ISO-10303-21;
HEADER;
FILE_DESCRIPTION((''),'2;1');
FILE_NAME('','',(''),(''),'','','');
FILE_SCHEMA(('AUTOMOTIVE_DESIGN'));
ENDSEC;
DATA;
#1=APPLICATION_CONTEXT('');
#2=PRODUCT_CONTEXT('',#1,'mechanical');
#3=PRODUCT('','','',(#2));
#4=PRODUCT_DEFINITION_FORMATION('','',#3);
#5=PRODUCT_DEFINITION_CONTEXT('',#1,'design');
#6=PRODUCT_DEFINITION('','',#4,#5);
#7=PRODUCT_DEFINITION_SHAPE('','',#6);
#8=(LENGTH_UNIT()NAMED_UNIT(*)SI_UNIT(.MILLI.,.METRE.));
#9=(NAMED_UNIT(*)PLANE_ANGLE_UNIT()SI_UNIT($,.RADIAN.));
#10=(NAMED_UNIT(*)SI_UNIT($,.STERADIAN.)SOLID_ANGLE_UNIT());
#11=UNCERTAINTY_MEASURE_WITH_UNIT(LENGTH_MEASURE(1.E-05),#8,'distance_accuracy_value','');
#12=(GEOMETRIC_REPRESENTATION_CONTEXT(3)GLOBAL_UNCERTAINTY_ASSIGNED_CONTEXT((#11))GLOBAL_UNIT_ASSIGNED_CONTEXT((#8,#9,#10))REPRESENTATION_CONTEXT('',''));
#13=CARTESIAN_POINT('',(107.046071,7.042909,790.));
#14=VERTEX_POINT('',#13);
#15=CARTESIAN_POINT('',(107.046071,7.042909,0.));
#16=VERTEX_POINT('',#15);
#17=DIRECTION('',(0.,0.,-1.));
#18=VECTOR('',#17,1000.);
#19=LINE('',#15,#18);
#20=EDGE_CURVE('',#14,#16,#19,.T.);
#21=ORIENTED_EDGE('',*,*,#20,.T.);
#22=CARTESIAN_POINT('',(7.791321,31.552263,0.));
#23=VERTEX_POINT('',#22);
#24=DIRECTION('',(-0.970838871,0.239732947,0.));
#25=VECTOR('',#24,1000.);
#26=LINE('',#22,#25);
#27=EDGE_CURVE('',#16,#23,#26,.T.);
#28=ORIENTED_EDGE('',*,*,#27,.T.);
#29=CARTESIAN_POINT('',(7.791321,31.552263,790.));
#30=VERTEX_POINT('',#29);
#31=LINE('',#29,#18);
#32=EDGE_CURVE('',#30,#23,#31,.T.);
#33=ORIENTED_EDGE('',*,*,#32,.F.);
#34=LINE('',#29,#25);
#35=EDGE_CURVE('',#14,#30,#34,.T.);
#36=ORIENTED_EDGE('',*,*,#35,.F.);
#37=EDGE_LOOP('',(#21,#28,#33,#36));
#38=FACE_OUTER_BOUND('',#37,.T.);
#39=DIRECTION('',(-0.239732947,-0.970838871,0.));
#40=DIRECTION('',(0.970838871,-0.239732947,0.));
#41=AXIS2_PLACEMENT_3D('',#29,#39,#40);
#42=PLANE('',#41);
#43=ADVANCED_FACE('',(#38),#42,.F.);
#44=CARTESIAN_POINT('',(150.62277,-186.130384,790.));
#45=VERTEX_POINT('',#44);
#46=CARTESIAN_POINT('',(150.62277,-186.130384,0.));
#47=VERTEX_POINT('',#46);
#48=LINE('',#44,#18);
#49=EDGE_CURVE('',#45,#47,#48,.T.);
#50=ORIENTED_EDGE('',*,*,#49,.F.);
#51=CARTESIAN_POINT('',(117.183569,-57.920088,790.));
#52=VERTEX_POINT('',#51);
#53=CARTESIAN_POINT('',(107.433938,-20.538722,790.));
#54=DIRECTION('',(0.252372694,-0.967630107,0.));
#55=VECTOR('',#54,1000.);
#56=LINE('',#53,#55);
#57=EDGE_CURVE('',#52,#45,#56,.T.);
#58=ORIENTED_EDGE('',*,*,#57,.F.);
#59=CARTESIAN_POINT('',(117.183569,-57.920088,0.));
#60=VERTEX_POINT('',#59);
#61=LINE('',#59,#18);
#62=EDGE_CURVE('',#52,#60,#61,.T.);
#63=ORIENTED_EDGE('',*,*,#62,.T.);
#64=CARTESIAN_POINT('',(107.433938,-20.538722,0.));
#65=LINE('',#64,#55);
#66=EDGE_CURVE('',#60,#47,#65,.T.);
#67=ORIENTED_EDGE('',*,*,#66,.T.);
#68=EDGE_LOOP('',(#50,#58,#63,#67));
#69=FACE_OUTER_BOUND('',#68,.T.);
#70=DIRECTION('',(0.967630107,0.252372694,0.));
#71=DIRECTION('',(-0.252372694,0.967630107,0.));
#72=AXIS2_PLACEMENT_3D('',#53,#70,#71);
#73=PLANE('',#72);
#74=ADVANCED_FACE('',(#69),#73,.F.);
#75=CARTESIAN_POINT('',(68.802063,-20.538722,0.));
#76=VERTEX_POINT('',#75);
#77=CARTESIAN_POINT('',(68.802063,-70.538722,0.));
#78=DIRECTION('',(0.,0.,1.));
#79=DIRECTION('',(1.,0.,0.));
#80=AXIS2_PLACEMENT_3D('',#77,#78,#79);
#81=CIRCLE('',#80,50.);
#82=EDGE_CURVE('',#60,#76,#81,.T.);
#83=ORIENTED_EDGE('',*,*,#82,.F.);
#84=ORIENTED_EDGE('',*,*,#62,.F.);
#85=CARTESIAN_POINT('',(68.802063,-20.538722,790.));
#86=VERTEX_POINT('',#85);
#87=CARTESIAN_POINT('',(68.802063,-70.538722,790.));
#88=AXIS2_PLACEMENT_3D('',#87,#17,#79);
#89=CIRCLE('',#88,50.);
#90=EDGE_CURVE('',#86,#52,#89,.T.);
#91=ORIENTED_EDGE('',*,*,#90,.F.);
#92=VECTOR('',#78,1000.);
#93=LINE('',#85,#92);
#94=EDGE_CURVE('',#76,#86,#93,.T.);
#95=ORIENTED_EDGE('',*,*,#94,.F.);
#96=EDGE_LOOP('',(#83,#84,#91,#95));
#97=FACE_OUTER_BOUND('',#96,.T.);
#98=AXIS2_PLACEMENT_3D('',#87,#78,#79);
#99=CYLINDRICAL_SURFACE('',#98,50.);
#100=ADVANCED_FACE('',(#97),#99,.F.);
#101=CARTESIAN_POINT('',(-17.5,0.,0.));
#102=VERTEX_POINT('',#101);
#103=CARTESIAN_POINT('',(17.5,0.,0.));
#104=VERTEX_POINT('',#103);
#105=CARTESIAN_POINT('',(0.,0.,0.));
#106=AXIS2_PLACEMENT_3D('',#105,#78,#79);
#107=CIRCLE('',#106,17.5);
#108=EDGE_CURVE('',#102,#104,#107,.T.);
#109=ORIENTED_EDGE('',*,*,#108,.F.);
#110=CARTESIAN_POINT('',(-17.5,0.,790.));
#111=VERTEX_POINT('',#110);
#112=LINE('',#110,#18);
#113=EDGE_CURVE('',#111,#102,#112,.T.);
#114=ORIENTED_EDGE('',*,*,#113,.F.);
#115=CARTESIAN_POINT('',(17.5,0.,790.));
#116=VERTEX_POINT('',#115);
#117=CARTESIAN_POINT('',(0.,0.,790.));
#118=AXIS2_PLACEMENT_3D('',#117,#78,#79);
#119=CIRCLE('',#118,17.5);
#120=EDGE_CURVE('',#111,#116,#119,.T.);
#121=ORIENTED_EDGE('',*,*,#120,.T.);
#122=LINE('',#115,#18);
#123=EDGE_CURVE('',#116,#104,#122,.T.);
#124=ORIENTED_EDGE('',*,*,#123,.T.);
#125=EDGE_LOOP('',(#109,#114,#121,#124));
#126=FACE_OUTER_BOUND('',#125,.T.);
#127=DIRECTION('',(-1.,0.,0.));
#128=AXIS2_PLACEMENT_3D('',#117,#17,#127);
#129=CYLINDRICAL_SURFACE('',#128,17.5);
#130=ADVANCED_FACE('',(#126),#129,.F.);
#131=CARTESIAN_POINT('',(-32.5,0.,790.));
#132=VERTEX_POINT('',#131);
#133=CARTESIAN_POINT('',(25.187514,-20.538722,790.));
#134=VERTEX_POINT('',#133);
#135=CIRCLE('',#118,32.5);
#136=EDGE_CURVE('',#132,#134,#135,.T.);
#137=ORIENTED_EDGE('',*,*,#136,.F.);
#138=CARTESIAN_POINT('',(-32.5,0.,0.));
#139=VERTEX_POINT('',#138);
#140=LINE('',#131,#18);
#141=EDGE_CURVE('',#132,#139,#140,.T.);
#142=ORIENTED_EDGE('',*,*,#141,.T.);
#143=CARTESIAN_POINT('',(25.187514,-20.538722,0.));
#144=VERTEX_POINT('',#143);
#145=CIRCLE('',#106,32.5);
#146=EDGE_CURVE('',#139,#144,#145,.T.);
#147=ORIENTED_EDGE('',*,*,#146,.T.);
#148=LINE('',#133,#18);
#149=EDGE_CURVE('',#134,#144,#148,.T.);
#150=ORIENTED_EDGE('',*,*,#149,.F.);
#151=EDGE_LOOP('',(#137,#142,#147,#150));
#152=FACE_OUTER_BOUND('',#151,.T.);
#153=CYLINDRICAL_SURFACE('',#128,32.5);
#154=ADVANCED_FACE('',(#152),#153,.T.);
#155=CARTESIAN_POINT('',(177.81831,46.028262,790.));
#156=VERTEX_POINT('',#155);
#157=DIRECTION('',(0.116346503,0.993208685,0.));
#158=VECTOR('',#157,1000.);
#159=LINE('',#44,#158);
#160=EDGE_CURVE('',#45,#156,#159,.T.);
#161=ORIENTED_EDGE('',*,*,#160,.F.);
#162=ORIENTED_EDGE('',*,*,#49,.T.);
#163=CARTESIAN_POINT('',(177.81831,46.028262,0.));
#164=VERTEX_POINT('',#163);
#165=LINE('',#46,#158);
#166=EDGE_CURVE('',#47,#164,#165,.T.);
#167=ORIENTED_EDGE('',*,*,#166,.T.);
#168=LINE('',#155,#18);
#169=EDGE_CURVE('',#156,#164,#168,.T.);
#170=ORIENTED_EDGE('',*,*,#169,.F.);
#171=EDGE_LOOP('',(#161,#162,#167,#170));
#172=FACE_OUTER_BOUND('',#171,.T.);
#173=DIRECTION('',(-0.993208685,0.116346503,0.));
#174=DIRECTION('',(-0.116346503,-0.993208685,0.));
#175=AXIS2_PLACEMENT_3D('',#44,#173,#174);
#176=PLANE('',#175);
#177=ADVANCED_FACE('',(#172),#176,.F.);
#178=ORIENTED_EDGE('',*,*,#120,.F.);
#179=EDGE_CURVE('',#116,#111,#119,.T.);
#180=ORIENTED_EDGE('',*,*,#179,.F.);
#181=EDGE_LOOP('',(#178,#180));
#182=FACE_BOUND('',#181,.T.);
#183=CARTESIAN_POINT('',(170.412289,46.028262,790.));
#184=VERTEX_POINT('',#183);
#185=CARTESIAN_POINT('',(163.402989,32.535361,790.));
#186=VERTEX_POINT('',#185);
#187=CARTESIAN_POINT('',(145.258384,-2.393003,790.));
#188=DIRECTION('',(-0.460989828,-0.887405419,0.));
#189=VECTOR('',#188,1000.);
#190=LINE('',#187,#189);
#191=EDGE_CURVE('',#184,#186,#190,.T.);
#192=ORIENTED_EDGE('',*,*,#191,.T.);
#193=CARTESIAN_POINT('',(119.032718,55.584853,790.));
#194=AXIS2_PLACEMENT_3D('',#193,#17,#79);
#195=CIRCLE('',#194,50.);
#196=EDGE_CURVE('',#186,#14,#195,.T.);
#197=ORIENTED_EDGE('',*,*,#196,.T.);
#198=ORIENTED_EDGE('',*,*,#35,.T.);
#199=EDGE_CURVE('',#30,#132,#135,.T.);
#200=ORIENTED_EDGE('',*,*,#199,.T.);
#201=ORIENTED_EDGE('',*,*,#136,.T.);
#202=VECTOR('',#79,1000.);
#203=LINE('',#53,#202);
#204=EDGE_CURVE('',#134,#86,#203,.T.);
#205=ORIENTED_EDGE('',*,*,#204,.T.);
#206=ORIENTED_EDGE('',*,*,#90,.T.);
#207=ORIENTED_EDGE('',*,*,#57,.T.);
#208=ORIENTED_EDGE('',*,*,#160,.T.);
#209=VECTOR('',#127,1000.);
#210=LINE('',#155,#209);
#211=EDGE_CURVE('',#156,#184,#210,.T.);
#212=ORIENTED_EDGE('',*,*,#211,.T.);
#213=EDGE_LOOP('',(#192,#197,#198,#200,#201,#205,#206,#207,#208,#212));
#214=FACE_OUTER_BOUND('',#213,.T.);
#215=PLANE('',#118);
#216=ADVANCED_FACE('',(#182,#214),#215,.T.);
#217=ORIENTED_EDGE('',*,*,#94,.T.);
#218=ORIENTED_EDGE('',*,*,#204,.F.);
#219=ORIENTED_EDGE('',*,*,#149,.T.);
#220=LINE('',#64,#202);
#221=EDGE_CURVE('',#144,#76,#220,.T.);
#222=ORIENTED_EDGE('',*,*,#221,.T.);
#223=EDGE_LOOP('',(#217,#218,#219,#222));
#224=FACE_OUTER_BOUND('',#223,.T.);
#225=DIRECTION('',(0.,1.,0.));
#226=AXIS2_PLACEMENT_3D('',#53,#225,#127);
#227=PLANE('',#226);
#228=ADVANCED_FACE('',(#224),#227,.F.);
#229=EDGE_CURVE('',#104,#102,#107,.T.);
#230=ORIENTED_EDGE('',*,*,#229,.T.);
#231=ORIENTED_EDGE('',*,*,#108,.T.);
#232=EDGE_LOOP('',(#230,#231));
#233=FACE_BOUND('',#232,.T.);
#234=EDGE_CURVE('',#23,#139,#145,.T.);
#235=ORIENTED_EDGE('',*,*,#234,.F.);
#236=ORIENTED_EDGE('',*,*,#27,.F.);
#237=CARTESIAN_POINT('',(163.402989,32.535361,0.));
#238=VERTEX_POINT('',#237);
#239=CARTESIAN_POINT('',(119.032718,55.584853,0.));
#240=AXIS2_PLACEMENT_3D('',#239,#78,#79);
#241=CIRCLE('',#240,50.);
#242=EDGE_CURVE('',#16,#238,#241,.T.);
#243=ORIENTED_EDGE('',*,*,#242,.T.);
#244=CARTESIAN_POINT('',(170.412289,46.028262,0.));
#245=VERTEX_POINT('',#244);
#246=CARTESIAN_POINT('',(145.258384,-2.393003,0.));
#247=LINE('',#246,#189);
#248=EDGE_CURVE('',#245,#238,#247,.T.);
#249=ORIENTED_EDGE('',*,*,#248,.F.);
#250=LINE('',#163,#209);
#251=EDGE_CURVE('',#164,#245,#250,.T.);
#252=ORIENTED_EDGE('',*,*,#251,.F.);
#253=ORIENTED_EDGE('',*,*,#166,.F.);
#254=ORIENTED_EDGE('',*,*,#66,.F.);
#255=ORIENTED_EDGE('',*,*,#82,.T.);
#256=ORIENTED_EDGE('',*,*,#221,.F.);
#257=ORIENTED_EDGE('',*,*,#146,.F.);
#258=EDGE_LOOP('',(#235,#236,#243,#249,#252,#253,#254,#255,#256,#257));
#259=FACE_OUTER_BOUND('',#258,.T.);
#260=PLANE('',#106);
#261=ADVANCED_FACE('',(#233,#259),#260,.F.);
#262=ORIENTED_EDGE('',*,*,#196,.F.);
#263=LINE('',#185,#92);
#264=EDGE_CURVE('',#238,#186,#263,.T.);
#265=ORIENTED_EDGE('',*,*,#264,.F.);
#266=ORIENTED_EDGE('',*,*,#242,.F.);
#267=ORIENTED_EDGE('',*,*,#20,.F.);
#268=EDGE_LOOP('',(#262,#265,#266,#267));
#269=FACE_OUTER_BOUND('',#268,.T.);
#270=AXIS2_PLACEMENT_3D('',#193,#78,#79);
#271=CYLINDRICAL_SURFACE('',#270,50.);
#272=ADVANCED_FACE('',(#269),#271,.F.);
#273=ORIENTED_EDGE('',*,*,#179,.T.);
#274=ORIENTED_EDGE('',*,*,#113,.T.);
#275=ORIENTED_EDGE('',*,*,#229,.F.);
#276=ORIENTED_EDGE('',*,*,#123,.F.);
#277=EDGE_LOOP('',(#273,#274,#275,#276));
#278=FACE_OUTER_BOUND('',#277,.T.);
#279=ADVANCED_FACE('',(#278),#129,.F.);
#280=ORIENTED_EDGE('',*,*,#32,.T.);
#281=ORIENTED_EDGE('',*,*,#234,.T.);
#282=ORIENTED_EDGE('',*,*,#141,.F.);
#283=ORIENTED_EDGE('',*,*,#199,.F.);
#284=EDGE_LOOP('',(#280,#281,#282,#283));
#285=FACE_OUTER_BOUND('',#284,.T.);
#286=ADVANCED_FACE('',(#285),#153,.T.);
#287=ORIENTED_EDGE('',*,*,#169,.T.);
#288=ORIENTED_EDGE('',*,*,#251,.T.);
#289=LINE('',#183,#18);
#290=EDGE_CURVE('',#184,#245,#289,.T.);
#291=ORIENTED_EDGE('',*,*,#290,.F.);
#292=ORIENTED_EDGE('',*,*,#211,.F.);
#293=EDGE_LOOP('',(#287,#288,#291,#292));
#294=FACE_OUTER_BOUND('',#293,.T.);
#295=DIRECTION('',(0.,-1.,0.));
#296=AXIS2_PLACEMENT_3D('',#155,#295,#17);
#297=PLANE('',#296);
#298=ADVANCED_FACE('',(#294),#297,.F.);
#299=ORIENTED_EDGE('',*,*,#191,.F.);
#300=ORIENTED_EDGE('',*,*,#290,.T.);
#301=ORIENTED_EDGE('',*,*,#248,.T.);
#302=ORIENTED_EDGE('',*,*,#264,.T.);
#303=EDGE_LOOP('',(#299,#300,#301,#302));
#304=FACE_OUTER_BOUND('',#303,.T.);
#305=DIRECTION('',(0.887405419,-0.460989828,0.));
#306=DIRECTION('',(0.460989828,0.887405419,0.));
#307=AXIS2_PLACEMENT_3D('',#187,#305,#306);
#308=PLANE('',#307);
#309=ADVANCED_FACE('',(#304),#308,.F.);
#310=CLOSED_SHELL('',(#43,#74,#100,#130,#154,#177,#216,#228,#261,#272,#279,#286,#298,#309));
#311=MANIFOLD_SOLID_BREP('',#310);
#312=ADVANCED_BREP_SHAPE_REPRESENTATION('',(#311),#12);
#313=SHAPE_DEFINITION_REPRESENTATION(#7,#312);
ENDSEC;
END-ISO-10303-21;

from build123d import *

# Parameters (mm, degrees)
SKETCH1_R           = 17.5
BOSS_EXTRUDE1_DEPTH = 790
FILLET1_R           = 50
FILLET3_R           = 50


with BuildPart() as part:
    # Sketch1 → Boss-Extrude1 (new body)
    with BuildSketch(Plane.XY):
        with BuildLine():
            Line((7.791320793, 31.552263315), (145.258384303, -2.393003291))
            Line((145.258384303, -2.393003291), (170.412288606, 46.028262492))
            Line((170.412288606, 46.028262492), (177.818310073, 46.028262492))
            Line((177.818310073, 46.028262492), (150.622769958, -186.130384226))
            Line((150.622769958, -186.130384226), (107.433938335, -20.538722405))
            Line((107.433938335, -20.538722405), (25.187514406, -20.538722405))
            ThreePointArc((25.187514406, -20.538722405), (-30.82642683, -10.294727238), (7.791320793, 31.552263315))
        make_face()
        with Locations(Location((0, 0, 0), (0, 0, 180))):
            Circle(SKETCH1_R, mode=Mode.SUBTRACT)
    extrude(amount=BOSS_EXTRUDE1_DEPTH)

    # Fillet1
    fillet1_edges = [part.edges().sort_by_distance(p)[0] for p in [
        (145.258384303, -2.393003291, 395),
    ]]
    fillet(fillet1_edges, radius=FILLET1_R)

    # Fillet3
    fillet3_edges = [part.edges().sort_by_distance(p)[0] for p in [
        (107.433938335, -20.538722405, 395),
    ]]
    fillet(fillet3_edges, radius=FILLET3_R)


solid = part.part
